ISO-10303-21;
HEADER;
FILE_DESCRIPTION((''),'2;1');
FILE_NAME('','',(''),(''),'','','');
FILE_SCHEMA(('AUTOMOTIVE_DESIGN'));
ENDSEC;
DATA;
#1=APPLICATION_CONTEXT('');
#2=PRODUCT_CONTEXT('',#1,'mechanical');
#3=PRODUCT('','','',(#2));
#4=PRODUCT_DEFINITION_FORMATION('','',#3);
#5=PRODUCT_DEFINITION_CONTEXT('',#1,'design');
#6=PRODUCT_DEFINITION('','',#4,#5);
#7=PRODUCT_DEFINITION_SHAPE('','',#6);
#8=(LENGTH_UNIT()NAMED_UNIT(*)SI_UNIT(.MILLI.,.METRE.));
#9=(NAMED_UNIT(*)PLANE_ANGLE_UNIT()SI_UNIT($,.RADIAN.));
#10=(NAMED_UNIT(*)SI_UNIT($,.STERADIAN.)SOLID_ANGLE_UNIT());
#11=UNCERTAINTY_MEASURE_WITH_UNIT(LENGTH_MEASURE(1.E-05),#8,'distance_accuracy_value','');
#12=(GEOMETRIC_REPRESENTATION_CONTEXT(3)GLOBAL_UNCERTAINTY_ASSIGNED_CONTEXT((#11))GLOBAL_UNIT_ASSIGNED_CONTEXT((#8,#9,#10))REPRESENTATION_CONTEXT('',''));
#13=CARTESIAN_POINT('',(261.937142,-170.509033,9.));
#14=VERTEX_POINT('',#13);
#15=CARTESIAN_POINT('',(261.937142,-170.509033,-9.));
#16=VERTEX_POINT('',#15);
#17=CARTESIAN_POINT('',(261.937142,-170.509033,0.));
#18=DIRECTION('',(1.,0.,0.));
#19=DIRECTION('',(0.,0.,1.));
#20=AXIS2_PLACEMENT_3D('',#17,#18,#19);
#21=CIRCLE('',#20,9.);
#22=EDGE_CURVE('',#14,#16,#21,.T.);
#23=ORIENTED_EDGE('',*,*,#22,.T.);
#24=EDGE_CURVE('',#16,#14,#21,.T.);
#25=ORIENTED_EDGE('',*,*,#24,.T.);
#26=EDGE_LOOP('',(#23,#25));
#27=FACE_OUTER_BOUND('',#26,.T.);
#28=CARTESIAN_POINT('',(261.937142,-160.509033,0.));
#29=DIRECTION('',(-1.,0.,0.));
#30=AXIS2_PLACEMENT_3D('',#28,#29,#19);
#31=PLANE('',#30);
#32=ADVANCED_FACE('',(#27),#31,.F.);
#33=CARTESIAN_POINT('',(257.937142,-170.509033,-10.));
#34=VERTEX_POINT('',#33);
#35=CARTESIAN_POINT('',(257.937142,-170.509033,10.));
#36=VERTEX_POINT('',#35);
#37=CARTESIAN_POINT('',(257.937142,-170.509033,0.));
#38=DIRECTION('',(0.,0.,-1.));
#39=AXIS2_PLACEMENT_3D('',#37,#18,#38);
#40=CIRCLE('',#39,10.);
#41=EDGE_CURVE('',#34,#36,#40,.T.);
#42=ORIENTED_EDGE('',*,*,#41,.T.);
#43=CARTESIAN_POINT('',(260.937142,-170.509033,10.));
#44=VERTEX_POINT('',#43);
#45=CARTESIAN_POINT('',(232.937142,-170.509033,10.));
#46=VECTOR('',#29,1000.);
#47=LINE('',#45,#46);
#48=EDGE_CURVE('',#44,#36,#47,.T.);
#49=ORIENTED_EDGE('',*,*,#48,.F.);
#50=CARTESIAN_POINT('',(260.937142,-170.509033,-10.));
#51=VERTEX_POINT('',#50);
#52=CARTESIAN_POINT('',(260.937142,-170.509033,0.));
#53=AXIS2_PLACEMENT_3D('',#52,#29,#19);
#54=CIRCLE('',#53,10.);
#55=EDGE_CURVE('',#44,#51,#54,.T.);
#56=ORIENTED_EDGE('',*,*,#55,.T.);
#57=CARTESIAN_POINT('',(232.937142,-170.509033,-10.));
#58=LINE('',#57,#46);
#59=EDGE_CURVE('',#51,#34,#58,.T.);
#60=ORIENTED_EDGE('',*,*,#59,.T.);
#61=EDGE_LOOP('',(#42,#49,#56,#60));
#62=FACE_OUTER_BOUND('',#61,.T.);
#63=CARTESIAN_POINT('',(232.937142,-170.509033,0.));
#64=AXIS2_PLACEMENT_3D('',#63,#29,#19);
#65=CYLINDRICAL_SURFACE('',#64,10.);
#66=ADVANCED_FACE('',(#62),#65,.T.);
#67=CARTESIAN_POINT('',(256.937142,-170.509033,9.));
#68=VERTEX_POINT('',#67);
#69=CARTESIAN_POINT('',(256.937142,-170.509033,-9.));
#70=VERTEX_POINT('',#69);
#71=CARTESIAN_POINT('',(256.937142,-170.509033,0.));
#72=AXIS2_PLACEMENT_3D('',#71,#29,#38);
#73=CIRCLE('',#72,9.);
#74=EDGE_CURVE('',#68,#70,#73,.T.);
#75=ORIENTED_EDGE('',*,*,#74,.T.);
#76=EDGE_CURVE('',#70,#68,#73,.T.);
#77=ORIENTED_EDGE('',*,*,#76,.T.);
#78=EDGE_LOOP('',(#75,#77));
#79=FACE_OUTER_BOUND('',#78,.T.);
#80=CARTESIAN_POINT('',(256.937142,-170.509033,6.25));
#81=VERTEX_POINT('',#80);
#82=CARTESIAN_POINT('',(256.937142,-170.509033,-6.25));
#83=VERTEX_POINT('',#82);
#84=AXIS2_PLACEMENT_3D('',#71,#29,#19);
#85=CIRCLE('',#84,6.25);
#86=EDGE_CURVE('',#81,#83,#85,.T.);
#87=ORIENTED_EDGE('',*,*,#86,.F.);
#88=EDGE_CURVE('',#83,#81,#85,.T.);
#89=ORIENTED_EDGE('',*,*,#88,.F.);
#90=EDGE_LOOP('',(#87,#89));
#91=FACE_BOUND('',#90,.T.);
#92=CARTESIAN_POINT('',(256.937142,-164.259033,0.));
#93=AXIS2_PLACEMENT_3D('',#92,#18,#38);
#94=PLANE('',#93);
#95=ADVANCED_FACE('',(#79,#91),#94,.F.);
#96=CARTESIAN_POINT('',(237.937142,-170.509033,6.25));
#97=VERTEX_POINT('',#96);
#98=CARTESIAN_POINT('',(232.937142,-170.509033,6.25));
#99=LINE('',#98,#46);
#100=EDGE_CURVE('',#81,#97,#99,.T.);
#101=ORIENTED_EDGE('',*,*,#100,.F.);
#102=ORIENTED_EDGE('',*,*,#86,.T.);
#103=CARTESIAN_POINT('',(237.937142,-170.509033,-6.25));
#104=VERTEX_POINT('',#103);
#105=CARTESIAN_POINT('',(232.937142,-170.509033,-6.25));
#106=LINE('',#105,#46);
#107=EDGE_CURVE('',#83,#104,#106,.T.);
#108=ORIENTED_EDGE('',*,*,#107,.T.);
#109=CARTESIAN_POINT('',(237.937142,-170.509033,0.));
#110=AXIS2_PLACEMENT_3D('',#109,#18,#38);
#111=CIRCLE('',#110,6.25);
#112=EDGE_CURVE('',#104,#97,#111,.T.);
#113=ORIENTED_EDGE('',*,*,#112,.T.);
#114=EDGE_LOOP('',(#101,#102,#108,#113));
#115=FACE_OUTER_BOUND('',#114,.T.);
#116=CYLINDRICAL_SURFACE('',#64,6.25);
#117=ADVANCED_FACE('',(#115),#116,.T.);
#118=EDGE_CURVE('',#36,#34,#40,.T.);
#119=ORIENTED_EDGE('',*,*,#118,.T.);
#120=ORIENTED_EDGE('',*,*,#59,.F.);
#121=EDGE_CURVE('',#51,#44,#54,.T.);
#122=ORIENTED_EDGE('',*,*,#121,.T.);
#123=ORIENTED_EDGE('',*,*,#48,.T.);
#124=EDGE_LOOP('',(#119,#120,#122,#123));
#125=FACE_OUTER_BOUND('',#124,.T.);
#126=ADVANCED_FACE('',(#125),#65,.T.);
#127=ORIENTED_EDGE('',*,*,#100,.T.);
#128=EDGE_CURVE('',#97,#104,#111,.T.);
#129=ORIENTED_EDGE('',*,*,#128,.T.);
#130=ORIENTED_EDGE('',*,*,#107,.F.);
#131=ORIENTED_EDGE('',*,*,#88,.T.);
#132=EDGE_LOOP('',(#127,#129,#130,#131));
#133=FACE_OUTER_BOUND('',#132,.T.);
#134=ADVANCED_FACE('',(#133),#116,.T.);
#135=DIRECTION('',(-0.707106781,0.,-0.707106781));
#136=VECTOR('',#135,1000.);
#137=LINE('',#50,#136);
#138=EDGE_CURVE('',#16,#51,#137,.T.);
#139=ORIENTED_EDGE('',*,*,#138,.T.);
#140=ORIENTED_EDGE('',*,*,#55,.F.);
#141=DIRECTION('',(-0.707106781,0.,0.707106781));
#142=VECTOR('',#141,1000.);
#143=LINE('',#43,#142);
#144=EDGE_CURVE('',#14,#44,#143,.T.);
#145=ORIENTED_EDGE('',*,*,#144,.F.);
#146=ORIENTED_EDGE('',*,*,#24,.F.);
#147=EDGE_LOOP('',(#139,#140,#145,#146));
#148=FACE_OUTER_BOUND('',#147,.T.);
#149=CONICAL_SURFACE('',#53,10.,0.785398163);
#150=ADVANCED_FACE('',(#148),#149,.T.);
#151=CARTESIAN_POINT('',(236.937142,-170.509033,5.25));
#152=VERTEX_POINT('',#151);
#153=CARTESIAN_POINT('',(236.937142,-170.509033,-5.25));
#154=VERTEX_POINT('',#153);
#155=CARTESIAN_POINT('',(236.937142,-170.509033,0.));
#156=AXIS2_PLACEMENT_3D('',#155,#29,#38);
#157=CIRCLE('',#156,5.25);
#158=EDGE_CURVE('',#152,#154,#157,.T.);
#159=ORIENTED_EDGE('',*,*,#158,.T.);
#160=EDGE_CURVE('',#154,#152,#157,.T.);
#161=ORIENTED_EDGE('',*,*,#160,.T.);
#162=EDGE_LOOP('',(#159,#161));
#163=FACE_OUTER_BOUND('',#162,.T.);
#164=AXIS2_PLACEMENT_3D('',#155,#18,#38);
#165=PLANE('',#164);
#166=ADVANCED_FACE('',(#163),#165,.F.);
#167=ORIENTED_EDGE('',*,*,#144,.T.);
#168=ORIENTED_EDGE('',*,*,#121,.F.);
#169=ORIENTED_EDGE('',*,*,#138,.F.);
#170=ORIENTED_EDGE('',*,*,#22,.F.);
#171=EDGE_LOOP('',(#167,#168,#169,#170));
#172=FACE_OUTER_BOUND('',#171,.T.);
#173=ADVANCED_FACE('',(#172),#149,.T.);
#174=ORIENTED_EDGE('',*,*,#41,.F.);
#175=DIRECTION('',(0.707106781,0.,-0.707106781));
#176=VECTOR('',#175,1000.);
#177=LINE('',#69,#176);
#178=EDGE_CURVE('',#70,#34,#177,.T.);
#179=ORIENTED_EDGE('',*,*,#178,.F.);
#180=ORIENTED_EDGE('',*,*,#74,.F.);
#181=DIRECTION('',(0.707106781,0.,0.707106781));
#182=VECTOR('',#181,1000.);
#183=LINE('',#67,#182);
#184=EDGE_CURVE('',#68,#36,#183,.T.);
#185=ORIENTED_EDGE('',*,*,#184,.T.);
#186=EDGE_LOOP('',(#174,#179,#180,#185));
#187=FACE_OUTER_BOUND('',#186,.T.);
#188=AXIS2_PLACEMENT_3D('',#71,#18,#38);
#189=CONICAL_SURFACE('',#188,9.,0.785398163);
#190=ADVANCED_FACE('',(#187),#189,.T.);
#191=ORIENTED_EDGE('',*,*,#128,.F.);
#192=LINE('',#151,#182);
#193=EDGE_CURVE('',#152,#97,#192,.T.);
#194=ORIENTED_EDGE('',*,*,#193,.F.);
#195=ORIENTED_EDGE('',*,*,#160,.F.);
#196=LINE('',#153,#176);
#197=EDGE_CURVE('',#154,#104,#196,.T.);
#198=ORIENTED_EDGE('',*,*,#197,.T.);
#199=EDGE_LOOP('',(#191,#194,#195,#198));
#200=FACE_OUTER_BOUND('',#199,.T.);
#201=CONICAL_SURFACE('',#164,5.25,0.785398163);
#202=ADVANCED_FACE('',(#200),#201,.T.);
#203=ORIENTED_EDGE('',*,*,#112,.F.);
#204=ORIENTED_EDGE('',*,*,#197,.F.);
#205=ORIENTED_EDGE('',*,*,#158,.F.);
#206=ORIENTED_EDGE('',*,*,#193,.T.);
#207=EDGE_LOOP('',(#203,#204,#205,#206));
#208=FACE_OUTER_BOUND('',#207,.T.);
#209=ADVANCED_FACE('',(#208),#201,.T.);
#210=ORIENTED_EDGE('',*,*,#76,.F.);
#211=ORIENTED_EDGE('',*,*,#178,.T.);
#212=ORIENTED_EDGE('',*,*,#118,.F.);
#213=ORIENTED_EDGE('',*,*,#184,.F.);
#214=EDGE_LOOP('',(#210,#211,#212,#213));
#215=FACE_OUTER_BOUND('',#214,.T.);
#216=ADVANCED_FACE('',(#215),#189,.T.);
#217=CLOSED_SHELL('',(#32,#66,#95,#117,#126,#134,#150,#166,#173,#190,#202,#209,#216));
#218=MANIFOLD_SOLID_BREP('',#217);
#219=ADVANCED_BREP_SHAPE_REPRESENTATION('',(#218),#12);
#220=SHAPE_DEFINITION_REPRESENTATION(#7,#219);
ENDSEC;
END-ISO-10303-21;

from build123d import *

# Parameters (mm, degrees)
CHAMFER_1_SIZE = 1


with BuildPart() as part:
    # 草图1 → 旋转1 (revolve)
    with BuildSketch(Plane.XY, mode=Mode.PRIVATE) as revolve_1_sk:
        Polygon((236.937142185, -170.509032878), (236.937142185, -164.259032878), (256.937142185, -164.259032878), (256.937142185, -160.509032878), (261.937142185, -160.509032878), (261.937142185, -170.509032878), align=None)
    revolve(revolve_1_sk.sketch.rotate(Axis((232.937142185, -170.509032878, 0), (1, 0, 0)), 90), axis=Axis((232.937142185, -170.509032878, 0), (1, 0, 0)))

    # 倒角1
    chamfer_1_edges = [part.edges().sort_by_distance(p)[0] for p in [
        (261.937142185, -170.509032878, -10),
        (256.937142185, -170.509032878, -10),
        (236.937142185, -170.509032878, -6.25),
    ]]
    chamfer(chamfer_1_edges, length=CHAMFER_1_SIZE)


solid = part.part
